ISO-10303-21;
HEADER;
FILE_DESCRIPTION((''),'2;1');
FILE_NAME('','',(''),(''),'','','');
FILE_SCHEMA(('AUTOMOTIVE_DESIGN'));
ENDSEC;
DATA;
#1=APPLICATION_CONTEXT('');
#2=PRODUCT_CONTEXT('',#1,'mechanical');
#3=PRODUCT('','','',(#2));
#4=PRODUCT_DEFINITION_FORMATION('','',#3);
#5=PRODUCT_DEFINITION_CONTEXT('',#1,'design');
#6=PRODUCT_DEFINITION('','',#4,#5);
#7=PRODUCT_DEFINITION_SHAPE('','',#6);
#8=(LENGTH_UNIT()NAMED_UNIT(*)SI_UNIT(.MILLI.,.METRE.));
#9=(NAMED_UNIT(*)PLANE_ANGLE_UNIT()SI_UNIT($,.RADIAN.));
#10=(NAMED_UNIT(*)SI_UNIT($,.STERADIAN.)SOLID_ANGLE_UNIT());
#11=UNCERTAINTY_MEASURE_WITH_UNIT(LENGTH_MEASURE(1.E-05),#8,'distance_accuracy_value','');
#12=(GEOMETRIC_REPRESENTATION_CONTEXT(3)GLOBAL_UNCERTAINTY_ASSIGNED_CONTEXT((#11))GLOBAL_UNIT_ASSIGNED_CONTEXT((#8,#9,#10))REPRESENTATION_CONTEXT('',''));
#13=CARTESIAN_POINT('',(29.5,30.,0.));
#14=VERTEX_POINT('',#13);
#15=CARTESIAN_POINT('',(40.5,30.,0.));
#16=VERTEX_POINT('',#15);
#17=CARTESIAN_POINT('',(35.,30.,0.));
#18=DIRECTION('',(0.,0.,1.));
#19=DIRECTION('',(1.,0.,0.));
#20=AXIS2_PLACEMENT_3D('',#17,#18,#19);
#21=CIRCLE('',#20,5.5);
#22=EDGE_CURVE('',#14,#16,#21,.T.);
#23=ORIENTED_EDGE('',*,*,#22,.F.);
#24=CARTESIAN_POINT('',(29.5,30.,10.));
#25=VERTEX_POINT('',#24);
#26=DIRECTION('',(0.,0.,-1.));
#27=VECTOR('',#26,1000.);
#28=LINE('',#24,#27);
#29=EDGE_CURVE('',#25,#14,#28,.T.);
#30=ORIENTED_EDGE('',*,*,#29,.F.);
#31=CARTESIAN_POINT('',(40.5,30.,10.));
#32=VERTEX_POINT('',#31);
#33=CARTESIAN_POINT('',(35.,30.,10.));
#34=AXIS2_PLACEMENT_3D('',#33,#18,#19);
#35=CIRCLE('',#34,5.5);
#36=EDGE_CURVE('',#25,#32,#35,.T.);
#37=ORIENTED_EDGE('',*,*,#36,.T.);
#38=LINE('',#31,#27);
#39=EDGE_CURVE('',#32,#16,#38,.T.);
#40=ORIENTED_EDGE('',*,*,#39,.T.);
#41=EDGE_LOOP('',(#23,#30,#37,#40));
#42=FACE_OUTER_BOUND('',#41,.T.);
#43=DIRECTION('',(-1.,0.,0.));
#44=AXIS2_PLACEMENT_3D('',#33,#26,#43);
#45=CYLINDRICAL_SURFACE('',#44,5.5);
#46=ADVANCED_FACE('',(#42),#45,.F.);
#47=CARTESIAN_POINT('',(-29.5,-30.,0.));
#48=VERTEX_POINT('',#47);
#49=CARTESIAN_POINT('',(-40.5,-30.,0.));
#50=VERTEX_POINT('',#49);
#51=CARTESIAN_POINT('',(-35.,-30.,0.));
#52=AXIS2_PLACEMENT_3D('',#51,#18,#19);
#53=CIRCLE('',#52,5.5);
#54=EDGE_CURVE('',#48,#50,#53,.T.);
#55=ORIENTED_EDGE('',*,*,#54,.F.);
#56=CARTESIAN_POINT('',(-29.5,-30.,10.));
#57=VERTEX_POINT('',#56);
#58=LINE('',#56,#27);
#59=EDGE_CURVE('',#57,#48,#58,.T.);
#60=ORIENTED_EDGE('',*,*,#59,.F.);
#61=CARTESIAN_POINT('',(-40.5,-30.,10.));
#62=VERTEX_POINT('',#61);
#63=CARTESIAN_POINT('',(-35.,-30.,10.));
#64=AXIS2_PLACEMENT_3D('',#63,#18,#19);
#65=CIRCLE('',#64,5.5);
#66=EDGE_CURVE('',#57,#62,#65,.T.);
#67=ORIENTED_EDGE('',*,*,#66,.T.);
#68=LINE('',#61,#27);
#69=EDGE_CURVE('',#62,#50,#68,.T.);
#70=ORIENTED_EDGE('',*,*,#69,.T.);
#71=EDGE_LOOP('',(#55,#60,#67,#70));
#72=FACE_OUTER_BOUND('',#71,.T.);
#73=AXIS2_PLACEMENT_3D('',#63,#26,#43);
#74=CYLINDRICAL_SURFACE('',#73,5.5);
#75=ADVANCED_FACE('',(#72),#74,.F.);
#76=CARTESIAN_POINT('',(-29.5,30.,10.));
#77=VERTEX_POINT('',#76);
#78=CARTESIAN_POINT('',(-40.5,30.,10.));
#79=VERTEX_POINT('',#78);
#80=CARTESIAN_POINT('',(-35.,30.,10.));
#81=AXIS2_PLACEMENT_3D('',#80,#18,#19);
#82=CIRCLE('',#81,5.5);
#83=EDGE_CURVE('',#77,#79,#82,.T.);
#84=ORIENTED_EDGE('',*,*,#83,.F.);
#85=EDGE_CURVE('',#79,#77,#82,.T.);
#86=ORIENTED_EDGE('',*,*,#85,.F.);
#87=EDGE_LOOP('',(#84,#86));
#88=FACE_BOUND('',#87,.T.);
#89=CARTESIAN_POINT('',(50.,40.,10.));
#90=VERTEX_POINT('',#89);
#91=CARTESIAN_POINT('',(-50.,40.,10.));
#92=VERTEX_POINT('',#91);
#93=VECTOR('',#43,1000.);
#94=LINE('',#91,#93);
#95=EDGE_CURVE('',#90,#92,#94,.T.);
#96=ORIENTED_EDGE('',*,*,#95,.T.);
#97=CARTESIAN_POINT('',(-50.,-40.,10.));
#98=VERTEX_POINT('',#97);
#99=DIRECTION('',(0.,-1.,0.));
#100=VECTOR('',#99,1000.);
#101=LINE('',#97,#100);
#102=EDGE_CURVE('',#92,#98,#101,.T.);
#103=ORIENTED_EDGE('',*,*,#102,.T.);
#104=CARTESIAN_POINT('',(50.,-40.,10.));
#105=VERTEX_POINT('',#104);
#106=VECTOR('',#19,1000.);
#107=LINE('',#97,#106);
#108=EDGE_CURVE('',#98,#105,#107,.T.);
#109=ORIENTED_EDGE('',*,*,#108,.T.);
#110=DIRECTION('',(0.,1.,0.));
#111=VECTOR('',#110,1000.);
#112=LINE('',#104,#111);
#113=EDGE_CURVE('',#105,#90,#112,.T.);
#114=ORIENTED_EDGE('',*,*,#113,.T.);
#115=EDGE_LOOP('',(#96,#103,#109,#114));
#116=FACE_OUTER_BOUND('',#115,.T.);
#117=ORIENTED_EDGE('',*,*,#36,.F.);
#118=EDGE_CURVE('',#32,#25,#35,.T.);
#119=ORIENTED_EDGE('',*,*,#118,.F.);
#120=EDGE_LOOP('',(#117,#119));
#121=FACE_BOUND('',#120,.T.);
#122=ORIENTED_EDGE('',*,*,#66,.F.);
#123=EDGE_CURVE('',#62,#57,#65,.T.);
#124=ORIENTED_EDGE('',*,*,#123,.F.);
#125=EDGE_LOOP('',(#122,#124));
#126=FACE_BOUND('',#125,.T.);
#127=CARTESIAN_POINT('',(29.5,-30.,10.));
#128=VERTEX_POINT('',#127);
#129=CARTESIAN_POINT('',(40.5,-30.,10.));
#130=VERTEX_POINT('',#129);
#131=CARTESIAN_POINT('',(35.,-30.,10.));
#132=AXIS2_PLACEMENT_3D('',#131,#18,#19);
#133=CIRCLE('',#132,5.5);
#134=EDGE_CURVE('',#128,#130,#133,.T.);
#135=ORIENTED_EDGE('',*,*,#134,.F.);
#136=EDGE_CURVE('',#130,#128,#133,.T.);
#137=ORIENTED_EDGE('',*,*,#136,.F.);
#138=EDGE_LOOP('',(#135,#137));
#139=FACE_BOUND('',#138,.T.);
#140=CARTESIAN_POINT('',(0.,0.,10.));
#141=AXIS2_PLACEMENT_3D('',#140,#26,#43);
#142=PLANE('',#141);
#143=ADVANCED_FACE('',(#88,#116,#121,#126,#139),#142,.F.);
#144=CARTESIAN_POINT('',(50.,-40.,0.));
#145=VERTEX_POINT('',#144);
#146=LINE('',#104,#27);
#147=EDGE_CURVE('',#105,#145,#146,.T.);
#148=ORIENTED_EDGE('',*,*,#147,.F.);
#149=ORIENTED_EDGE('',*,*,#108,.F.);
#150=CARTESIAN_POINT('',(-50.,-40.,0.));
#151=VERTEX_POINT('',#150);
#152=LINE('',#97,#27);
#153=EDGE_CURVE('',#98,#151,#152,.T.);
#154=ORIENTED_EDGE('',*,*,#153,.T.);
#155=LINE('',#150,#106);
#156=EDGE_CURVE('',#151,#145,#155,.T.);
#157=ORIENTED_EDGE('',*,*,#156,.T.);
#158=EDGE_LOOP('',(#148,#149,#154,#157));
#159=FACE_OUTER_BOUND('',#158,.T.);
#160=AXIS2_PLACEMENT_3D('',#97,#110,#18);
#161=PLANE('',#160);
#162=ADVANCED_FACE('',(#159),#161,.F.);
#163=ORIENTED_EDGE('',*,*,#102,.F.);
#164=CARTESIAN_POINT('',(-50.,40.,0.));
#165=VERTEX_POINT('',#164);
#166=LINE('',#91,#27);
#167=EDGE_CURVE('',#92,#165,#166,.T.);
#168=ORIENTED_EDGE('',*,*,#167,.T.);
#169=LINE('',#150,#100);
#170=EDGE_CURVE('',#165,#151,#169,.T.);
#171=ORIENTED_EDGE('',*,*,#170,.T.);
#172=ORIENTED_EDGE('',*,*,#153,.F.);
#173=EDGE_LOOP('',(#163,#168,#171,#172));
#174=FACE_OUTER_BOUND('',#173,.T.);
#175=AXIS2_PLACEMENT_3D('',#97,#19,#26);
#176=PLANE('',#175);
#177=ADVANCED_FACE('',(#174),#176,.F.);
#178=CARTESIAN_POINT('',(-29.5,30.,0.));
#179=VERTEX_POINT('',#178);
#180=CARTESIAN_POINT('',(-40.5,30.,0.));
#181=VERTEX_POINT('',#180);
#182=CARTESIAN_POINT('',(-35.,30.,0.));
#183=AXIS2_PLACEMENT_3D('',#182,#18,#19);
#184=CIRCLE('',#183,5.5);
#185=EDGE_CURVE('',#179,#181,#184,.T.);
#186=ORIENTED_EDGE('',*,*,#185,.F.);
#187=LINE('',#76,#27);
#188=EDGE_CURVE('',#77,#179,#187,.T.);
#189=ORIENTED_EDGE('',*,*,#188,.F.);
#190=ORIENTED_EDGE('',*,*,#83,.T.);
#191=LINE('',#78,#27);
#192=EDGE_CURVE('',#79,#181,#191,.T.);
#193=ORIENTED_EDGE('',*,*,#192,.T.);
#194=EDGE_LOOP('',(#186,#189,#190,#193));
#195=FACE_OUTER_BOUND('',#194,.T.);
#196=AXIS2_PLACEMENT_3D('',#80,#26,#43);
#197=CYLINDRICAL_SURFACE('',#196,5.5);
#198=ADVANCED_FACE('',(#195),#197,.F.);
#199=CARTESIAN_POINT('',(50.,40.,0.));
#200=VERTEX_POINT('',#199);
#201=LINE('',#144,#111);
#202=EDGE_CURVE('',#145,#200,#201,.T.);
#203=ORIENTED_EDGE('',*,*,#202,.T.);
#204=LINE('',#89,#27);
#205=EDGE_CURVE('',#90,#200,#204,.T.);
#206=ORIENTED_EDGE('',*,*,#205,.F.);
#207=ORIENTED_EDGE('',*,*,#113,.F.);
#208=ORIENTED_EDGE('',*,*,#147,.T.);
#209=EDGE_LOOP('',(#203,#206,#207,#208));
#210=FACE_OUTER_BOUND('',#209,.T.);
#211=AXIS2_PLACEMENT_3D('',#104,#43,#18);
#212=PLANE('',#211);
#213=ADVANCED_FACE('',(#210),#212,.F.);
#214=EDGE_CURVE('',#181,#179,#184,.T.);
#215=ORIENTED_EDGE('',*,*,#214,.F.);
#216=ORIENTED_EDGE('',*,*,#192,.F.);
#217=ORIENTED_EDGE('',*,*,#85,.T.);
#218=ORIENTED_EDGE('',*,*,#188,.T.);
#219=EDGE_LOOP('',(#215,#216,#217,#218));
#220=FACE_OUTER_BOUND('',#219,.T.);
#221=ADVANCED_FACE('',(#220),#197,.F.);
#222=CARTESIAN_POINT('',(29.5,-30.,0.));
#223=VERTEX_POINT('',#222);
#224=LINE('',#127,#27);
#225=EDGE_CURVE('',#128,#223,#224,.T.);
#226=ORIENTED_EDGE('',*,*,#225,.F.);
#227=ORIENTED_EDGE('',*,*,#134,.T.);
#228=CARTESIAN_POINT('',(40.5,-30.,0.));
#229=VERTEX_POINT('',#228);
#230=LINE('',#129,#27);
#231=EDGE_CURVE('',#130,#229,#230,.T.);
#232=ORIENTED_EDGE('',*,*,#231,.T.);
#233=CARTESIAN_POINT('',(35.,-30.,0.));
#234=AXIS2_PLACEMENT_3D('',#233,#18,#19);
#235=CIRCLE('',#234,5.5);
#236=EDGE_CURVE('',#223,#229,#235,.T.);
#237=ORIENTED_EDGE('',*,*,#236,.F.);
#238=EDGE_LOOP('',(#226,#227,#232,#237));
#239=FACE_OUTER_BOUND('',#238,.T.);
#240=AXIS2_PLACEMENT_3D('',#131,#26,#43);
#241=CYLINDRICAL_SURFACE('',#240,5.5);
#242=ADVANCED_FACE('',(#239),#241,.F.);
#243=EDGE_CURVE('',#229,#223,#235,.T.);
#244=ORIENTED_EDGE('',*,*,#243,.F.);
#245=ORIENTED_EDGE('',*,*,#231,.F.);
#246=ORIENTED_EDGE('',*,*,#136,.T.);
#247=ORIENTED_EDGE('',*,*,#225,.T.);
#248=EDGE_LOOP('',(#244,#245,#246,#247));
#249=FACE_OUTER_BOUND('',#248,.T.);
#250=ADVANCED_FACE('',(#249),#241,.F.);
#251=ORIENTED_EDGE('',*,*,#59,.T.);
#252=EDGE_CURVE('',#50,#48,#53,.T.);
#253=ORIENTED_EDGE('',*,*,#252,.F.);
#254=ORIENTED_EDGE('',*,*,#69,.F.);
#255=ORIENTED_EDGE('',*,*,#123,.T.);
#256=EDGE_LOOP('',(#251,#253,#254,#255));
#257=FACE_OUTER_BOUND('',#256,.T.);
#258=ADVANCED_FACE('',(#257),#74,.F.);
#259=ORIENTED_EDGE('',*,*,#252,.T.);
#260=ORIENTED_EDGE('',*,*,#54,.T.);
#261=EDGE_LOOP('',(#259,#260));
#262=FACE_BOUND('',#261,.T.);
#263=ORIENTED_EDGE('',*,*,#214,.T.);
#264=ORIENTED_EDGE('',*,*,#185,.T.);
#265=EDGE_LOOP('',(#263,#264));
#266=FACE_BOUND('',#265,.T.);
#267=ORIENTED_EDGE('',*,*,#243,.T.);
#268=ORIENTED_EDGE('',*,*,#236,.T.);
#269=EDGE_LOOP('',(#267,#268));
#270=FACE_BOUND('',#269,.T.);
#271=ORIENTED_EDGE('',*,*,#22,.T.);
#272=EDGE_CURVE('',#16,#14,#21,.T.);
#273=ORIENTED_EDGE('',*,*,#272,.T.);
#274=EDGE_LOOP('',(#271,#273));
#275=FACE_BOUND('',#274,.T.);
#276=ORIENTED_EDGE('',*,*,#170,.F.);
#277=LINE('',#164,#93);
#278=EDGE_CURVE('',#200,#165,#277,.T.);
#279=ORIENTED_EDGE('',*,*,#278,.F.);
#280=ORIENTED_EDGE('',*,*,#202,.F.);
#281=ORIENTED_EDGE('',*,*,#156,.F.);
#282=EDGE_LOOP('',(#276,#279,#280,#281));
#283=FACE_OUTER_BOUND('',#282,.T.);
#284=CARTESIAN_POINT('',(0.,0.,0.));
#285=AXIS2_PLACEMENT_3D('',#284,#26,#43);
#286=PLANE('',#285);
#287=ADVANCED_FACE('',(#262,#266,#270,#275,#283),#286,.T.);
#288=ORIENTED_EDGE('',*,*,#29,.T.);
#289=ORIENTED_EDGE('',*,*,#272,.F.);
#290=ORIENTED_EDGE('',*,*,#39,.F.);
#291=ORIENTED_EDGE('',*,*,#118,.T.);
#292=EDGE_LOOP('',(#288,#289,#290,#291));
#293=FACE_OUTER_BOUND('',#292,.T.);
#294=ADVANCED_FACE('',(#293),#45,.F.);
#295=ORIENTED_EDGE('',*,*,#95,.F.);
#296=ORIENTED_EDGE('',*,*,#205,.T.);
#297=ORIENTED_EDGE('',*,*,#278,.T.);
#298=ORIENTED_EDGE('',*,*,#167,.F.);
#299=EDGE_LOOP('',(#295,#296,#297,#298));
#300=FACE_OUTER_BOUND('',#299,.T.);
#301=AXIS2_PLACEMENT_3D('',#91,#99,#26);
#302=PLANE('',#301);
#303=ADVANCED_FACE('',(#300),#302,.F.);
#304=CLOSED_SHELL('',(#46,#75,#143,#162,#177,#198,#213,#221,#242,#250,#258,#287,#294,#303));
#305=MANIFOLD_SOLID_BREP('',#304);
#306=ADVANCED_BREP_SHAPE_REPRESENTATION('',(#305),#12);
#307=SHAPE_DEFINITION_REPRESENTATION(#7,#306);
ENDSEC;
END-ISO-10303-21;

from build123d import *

# Parameters (mm, degrees)
SKETCH_1_W      = 100
SKETCH_1_H      = 80
SKETCH_1_R      = 5.5
EXTRUDE_1_DEPTH = 10


with BuildPart() as part:
    # 草图1 → 凸台-拉伸1 (new body)
    with BuildSketch(Plane.XY):
        Rectangle(SKETCH_1_W, SKETCH_1_H)
        with Locations((-35, 30)):
            Circle(SKETCH_1_R, mode=Mode.SUBTRACT)
        with Locations((-35, -30)):
            Circle(SKETCH_1_R, mode=Mode.SUBTRACT)
        with Locations((35, -30)):
            Circle(SKETCH_1_R, mode=Mode.SUBTRACT)
        with Locations((35, 30)):
            Circle(SKETCH_1_R, mode=Mode.SUBTRACT)
    extrude(amount=EXTRUDE_1_DEPTH)


solid = part.part
